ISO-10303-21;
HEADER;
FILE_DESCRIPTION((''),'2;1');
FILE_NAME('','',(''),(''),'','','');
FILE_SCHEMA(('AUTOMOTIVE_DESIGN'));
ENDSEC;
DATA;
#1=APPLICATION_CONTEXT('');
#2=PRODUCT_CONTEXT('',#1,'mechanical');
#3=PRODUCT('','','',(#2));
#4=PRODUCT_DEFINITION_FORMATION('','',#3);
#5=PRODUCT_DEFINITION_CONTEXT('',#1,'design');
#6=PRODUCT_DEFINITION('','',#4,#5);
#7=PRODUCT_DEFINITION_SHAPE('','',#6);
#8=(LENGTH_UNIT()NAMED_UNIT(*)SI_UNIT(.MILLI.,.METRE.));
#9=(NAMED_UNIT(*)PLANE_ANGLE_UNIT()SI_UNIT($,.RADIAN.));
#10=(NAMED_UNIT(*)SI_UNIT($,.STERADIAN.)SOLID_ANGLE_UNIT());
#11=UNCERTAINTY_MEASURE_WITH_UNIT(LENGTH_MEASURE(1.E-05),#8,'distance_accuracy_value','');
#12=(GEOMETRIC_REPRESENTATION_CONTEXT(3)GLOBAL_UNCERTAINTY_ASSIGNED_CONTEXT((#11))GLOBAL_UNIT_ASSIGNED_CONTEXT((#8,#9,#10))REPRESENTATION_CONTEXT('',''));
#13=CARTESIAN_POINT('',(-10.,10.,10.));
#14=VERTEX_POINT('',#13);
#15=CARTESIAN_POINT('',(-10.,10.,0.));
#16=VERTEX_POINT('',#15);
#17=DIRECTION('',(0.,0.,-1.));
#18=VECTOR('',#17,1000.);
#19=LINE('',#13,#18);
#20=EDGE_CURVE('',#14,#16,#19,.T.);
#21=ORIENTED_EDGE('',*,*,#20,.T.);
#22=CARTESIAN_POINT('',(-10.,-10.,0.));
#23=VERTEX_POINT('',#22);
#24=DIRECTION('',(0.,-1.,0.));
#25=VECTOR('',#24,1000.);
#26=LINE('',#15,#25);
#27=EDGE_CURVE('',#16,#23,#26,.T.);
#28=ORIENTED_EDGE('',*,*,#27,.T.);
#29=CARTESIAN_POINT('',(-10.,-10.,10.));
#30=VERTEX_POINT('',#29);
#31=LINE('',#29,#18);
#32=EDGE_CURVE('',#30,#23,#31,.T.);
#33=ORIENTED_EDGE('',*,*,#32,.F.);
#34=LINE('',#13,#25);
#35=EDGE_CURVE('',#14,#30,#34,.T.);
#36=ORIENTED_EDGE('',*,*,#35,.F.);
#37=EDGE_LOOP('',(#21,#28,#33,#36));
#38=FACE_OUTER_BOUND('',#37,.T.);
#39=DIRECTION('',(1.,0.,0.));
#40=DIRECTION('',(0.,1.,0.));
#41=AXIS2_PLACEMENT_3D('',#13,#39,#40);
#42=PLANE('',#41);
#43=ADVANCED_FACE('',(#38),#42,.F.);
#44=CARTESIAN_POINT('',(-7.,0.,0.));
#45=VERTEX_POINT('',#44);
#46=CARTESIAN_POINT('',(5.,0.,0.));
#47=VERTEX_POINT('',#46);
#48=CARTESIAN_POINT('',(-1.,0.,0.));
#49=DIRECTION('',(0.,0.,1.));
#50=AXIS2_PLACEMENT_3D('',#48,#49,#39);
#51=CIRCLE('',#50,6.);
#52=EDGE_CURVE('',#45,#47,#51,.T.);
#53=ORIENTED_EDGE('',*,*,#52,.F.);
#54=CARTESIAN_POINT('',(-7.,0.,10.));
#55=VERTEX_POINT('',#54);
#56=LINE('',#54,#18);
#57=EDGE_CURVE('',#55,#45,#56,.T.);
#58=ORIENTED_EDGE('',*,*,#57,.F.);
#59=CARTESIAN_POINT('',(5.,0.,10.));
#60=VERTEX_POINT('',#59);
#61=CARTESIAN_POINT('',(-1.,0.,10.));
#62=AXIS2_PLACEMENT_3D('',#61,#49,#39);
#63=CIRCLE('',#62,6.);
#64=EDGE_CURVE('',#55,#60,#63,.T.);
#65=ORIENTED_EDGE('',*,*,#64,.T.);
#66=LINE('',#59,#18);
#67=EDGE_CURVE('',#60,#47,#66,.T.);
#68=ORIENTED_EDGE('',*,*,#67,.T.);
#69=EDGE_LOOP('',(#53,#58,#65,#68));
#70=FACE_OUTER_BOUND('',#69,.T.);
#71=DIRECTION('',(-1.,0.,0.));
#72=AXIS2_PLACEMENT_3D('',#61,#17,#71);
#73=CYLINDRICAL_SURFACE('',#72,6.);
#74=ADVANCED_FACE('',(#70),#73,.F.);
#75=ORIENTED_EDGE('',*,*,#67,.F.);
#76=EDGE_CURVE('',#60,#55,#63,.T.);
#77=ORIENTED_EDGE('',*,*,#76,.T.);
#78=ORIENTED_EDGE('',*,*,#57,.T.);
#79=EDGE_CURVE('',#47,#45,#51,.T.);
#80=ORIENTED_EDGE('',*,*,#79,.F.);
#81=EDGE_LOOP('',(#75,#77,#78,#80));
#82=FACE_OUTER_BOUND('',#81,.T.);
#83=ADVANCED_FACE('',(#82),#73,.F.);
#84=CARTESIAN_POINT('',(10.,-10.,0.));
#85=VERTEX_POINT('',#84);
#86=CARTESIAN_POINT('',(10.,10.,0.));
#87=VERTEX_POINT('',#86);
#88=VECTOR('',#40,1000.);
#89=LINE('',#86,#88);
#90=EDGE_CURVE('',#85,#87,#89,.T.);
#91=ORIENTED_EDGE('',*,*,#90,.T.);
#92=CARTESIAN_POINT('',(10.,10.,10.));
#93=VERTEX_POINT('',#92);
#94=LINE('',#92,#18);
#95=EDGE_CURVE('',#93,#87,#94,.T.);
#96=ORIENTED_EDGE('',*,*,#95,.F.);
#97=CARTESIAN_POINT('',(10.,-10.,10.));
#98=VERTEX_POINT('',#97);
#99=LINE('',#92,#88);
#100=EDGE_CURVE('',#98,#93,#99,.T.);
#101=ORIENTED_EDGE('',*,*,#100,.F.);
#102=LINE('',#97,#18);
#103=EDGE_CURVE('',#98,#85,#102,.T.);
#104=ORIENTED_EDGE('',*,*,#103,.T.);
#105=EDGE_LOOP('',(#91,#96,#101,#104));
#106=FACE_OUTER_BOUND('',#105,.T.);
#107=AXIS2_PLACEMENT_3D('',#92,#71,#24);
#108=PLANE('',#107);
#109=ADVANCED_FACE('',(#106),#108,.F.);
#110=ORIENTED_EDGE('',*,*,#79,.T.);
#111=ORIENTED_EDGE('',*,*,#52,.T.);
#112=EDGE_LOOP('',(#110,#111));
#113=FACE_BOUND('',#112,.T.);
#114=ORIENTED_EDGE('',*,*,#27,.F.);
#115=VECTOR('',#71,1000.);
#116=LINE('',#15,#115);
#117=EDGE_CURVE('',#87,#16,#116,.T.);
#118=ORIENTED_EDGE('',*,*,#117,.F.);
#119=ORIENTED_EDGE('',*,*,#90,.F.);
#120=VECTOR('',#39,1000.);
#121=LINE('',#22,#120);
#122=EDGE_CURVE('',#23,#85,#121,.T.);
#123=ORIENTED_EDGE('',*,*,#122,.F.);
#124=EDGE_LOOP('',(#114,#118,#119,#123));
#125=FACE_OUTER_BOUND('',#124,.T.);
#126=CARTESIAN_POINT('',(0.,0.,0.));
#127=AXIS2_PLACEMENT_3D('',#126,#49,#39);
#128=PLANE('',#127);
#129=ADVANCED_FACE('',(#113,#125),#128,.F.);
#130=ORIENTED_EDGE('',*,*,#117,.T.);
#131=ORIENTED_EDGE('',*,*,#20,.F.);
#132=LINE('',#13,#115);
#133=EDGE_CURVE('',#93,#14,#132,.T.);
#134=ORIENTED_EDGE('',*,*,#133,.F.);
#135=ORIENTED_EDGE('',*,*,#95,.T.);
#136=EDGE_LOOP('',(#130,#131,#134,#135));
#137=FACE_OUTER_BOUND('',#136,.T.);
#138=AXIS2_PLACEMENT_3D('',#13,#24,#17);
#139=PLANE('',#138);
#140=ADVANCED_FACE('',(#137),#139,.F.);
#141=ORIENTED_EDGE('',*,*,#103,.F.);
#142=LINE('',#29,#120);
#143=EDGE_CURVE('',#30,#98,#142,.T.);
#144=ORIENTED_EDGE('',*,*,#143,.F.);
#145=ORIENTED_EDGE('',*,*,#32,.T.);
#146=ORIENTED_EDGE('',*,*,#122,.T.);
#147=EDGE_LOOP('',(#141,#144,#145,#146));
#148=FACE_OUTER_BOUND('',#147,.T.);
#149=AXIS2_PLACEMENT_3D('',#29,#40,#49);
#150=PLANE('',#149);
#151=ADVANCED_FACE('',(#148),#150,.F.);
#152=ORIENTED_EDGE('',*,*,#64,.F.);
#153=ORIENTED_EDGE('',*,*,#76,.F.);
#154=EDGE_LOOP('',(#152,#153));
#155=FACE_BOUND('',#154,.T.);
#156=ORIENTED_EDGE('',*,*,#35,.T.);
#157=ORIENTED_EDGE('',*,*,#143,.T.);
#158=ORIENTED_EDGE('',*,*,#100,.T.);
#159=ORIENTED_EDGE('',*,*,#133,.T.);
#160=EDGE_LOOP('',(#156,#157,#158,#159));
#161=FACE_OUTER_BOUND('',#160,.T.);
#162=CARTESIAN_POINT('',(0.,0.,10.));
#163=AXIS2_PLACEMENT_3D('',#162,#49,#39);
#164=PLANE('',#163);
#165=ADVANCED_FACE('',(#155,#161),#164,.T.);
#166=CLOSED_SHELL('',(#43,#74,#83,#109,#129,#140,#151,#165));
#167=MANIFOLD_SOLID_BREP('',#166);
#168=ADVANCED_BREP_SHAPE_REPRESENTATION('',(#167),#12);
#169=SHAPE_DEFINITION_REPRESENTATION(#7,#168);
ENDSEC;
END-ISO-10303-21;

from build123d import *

# Parameters (mm, degrees)
SKETCH1_W           = 20
SKETCH1_H           = 20
SKETCH1_R           = 6
BOSS_EXTRUDE1_DEPTH = 10


with BuildPart() as part:
    # Sketch1 → Boss-Extrude1 (new body)
    with BuildSketch(Plane.XY):
        Rectangle(SKETCH1_W, SKETCH1_H)
        with Locations((-1, 0)):
            Circle(SKETCH1_R, mode=Mode.SUBTRACT)
    extrude(amount=BOSS_EXTRUDE1_DEPTH)


solid = part.part
